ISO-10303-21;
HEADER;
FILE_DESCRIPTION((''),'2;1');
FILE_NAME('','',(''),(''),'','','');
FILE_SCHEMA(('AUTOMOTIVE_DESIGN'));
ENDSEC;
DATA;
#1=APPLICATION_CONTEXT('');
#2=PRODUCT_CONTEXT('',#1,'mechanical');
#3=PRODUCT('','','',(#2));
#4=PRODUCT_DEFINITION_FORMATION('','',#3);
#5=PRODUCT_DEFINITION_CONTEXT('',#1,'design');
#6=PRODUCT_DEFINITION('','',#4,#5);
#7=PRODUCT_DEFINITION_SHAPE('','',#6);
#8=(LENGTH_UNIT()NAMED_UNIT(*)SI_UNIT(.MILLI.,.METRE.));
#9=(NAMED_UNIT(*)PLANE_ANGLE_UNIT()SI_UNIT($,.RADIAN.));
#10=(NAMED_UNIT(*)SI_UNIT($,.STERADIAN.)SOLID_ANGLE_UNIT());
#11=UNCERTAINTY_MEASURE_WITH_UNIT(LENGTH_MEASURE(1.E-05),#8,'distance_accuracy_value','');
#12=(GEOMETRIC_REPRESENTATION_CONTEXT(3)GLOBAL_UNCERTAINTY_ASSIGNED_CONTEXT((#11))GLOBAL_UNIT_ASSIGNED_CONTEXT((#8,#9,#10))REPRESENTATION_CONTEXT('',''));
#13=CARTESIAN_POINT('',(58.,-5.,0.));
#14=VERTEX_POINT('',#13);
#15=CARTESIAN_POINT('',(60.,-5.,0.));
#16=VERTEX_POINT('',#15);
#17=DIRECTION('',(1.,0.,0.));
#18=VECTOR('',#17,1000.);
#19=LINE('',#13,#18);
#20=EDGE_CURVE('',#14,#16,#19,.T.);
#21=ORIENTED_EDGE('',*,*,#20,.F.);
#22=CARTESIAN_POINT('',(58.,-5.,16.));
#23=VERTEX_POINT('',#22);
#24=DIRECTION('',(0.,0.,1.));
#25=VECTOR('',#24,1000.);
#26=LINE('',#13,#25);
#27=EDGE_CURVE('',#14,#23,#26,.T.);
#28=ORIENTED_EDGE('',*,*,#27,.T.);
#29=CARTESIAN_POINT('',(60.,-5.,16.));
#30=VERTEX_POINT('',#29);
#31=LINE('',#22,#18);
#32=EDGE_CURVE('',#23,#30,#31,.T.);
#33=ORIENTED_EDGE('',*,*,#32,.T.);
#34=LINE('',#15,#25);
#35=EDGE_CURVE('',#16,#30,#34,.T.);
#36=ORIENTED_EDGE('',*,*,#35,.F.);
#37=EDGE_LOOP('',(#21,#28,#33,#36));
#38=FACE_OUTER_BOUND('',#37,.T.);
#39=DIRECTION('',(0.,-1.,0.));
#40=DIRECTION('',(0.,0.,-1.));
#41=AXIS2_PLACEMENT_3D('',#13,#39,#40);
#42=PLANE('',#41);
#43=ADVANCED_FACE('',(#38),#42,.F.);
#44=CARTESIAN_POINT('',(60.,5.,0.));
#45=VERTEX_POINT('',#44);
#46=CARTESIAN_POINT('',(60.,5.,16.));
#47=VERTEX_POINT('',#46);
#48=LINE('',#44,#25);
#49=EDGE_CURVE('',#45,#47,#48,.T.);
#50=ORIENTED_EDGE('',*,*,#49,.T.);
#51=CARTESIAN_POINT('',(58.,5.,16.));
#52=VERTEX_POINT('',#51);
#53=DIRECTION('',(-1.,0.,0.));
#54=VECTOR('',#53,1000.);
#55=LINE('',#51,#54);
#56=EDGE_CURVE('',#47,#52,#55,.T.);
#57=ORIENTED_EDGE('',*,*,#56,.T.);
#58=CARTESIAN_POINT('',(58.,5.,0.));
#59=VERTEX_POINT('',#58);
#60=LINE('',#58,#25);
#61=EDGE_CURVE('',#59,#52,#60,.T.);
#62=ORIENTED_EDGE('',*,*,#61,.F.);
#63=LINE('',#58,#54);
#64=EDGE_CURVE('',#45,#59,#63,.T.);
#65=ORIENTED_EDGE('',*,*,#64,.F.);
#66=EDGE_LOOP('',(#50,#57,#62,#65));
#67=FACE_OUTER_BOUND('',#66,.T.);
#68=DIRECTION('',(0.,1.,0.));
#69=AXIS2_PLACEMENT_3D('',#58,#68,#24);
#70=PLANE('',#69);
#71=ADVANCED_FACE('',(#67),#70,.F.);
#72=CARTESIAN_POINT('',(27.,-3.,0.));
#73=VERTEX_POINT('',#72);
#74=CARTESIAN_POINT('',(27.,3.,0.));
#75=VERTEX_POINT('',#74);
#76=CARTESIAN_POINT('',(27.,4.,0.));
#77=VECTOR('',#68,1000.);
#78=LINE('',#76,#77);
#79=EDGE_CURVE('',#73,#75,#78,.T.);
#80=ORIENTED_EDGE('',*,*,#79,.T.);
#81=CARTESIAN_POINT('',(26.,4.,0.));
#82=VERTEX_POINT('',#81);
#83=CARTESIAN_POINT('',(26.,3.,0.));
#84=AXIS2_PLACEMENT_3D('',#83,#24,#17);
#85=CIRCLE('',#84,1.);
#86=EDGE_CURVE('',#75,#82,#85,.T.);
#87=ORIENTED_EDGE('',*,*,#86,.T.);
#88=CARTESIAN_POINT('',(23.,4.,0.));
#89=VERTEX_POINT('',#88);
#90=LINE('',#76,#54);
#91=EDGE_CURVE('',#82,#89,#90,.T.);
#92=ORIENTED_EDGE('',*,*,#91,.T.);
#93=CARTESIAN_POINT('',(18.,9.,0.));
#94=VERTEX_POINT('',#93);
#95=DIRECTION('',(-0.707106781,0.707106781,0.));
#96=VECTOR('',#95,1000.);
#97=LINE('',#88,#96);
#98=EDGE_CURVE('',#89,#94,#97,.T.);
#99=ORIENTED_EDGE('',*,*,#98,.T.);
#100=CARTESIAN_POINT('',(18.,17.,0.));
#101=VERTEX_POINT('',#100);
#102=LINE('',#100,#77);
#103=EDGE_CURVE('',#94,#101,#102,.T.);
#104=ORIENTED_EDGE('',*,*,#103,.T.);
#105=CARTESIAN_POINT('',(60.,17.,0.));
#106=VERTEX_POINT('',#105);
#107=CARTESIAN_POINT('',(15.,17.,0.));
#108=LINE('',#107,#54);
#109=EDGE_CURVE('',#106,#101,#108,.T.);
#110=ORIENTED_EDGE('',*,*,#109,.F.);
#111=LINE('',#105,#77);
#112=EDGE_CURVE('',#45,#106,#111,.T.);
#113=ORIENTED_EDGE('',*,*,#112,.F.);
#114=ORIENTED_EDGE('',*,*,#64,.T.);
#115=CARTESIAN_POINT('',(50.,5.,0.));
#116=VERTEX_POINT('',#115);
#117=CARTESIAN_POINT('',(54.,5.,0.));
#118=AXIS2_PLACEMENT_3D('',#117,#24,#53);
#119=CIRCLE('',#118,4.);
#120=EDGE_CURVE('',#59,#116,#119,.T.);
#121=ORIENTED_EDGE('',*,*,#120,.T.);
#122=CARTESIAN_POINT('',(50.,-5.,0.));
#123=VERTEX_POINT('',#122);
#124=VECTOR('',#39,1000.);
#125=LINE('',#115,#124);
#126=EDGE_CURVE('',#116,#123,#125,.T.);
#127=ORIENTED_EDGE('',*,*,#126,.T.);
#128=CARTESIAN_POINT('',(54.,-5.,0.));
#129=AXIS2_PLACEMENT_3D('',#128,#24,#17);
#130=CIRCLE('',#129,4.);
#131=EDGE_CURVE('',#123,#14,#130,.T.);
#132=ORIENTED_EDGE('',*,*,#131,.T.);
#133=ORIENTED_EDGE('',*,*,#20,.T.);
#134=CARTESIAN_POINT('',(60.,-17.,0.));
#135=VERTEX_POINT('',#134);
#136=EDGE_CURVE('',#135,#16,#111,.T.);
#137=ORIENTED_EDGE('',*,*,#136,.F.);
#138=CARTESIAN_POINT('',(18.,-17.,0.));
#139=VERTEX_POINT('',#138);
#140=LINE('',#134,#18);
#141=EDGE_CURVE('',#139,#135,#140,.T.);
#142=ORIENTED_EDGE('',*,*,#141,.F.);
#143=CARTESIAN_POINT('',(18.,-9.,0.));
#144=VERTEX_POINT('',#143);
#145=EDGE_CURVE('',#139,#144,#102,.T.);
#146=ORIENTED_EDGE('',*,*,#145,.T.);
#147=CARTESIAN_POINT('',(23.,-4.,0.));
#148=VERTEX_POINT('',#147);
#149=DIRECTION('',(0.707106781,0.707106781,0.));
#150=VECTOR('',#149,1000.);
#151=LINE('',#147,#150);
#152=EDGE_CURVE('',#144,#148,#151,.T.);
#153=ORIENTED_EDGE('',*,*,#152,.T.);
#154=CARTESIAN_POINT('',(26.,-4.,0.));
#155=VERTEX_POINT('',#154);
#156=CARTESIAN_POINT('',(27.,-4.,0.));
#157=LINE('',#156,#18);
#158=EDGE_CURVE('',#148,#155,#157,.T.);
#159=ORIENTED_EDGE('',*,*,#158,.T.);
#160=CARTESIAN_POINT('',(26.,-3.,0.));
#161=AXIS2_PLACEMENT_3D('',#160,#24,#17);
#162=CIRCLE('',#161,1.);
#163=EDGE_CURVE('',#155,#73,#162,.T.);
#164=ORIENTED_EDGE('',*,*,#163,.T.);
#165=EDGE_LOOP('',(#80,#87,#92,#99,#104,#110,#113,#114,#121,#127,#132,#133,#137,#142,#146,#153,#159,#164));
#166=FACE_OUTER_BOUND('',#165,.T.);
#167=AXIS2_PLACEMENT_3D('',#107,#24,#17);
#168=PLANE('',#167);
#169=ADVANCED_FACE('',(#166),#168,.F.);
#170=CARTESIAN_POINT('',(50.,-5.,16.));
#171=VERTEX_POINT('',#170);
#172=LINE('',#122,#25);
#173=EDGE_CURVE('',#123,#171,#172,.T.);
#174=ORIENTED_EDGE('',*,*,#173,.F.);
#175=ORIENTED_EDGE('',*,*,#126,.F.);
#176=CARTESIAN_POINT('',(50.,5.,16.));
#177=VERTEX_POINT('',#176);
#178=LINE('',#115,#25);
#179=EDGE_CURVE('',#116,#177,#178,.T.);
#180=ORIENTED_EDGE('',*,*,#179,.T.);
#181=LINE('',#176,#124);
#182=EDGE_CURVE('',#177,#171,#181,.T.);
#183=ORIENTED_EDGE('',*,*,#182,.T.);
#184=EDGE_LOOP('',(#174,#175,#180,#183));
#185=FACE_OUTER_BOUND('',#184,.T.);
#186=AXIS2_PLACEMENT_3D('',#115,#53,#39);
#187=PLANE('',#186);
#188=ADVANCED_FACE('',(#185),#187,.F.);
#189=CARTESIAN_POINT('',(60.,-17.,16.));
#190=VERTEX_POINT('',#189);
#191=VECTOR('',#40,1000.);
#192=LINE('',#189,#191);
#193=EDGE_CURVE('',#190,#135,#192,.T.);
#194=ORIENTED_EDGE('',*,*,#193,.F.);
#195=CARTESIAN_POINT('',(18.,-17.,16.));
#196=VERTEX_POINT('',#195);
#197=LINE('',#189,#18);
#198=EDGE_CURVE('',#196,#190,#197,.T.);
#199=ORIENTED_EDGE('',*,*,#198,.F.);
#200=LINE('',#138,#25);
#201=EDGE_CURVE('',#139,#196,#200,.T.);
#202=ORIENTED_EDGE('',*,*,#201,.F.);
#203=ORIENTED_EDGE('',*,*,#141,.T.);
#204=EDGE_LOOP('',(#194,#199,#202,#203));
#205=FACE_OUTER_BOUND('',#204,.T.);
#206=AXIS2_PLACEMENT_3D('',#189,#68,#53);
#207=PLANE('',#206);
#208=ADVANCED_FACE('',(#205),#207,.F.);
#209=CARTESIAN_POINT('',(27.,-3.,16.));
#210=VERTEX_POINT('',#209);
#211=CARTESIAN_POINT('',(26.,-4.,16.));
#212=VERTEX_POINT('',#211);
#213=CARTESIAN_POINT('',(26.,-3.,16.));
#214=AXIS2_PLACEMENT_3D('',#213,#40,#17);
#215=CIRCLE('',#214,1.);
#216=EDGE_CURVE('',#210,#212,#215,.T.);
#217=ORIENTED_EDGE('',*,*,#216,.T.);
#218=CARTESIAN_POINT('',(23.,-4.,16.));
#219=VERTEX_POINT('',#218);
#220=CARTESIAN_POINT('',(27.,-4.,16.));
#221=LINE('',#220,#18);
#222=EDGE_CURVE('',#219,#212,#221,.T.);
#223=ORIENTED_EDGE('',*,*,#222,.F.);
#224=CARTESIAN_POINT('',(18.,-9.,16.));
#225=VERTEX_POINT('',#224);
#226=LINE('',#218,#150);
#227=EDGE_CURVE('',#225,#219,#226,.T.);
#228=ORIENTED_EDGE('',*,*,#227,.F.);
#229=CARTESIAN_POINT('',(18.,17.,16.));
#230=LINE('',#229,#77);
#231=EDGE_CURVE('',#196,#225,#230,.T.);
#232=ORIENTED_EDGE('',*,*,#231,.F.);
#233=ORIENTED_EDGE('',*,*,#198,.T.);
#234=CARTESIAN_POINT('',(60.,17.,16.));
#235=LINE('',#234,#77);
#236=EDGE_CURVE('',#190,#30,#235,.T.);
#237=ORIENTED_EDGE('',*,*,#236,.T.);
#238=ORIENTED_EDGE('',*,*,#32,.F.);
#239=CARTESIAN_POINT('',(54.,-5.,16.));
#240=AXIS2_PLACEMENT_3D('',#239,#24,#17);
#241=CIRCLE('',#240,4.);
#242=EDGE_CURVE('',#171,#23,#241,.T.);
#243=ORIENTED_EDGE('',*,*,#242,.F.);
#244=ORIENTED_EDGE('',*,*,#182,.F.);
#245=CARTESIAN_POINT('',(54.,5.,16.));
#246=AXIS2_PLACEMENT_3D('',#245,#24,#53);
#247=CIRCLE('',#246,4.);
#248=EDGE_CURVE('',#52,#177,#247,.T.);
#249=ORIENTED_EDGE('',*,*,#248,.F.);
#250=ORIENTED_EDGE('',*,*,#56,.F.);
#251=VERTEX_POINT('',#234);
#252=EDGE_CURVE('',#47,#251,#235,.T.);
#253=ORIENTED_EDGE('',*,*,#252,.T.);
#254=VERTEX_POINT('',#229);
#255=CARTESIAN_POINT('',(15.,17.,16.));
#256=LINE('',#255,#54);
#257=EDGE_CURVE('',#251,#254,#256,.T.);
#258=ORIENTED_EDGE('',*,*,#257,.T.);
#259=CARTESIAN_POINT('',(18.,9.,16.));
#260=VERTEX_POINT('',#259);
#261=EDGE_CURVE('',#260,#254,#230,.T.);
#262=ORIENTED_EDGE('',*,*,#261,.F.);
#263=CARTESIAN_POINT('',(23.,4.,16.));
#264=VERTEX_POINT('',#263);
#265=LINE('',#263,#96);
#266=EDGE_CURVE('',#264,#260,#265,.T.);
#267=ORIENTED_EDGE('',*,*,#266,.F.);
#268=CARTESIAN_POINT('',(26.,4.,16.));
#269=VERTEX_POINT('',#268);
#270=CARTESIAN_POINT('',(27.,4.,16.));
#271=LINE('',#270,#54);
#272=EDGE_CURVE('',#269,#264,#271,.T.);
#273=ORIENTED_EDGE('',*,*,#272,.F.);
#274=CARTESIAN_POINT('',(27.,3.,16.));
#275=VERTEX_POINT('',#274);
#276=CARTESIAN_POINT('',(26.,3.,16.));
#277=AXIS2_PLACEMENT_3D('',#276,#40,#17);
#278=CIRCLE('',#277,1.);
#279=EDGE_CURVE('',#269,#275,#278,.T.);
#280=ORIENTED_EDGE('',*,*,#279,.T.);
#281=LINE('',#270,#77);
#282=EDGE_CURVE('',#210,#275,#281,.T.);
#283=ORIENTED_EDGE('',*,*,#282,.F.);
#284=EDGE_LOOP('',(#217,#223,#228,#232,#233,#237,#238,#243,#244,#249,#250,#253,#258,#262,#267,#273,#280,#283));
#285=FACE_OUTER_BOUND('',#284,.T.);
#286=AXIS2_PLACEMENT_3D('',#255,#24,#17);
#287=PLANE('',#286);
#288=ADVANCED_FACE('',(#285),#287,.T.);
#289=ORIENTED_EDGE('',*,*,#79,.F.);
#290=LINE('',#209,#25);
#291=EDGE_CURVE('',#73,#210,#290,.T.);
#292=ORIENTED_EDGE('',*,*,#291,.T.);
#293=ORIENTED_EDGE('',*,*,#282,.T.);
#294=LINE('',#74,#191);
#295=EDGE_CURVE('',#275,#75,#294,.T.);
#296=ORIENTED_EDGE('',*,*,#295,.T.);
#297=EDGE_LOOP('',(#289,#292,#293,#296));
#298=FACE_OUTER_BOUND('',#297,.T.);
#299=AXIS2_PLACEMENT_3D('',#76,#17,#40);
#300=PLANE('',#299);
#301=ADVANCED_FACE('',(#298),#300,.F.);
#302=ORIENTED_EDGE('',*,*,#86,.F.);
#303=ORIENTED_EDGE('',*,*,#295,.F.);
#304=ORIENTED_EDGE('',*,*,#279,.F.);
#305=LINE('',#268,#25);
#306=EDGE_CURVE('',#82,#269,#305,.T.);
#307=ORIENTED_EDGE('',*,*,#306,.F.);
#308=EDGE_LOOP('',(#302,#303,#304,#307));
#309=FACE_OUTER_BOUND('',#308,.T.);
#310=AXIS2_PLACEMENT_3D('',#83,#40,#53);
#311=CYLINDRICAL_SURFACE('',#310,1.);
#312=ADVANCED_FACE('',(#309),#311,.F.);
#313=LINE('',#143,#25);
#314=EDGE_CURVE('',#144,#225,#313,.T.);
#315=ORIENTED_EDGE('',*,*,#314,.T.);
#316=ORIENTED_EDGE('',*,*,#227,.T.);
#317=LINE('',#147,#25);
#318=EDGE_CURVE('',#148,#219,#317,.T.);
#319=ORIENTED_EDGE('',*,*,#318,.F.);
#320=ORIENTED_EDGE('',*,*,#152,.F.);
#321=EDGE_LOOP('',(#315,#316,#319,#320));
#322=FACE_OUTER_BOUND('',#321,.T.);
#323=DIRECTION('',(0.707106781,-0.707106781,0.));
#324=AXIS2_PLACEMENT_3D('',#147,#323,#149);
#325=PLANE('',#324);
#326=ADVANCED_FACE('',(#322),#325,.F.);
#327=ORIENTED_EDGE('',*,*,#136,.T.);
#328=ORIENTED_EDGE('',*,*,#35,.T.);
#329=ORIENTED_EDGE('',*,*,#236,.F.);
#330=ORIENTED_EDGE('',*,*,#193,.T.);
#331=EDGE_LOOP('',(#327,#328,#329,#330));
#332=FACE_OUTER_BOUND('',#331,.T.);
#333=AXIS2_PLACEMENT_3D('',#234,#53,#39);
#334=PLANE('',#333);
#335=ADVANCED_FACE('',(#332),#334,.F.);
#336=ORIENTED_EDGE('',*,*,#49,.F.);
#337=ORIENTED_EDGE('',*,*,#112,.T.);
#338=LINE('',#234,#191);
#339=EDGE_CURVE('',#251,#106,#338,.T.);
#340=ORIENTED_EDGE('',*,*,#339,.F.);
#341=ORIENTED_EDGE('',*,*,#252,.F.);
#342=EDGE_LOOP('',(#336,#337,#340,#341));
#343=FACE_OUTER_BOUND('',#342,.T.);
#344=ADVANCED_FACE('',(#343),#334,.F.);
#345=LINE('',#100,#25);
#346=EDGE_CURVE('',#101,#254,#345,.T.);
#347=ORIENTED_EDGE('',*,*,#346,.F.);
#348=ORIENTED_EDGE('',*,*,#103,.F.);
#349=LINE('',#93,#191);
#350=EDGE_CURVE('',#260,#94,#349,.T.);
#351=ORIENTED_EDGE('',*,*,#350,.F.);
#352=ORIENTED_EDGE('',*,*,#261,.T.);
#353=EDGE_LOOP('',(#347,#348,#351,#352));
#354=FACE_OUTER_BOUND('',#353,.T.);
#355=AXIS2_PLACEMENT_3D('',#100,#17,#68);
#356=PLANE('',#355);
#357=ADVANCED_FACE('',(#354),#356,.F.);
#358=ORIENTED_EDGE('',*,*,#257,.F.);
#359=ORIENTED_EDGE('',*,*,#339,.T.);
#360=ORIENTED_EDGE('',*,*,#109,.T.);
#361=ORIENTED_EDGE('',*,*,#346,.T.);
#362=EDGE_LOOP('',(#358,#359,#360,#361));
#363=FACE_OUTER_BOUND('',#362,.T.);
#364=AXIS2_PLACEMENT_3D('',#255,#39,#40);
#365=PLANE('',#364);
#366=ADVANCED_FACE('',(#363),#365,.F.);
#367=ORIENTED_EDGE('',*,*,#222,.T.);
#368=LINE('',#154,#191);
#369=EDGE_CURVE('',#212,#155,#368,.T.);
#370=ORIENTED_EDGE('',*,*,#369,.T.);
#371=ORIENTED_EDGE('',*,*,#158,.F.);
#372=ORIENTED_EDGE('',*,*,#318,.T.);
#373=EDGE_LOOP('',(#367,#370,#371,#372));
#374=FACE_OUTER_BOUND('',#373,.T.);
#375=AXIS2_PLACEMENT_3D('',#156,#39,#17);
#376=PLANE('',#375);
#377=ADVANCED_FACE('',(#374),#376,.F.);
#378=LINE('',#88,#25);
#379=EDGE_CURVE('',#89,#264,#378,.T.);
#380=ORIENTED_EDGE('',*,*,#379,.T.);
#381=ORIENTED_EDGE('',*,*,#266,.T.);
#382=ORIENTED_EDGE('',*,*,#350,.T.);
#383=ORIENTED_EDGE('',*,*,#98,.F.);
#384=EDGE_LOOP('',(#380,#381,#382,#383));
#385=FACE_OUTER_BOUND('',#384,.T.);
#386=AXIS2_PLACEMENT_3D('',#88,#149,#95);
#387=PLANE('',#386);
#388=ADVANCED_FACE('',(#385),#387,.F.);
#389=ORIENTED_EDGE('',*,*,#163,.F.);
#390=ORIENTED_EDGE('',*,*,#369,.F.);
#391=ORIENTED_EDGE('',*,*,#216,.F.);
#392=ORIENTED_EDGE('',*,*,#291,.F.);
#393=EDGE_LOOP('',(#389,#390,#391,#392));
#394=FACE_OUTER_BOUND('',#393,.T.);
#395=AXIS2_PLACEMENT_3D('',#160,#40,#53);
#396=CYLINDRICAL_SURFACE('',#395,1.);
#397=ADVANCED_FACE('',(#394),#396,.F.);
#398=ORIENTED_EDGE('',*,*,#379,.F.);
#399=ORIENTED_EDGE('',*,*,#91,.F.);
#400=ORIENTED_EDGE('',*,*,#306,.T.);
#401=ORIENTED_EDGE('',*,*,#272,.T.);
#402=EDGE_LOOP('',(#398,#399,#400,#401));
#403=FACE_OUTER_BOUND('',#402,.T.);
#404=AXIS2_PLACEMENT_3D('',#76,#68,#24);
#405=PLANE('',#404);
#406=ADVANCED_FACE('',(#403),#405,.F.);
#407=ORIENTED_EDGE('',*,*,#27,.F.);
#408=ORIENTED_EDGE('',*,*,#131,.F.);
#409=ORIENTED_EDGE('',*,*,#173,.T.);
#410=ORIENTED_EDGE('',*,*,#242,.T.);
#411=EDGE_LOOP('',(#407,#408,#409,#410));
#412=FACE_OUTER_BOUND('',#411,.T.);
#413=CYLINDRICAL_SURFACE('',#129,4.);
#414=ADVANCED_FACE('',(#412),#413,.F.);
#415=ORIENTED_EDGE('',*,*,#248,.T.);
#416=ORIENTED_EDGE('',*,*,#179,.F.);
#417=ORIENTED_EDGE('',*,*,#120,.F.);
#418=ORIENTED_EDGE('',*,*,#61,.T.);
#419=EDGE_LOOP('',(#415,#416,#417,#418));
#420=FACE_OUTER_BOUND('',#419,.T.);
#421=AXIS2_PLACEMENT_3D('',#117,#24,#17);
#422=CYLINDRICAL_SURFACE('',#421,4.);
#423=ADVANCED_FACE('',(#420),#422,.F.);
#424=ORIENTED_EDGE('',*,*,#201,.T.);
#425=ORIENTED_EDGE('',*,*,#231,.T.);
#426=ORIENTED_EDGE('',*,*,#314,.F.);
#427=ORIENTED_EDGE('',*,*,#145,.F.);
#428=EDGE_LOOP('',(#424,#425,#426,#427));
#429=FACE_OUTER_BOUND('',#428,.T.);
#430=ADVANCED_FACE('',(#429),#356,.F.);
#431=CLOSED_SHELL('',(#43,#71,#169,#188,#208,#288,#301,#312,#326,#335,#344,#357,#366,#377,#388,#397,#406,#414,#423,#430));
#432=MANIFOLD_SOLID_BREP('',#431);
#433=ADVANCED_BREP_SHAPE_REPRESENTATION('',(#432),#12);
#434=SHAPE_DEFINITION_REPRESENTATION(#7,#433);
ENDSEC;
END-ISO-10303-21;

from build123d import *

# Parameters (mm, degrees)
SKETCH1_W          = 45
SKETCH1_H          = 34
BASE_EXTRUDE_DEPTH = 16
CUT_EXTRUDE1_DEPTH = 65.381674411
FILLET1_R          = 1
FILLET2_R          = 1
CUT_EXTRUDE3_DEPTH = 65.381674411
SKETCH5_W          = 3
SKETCH5_H          = 34
CUT_EXTRUDE4_DEPTH = 65.381674411


with BuildPart() as part:
    # Sketch1 → Base-Extrude (new body)
    with BuildSketch(Plane.XY):
        with Locations((37.5, 0)):
            Rectangle(SKETCH1_W, SKETCH1_H)
    extrude(amount=BASE_EXTRUDE_DEPTH)

    # Sketch2 → Cut-Extrude1 (cut, through all)
    with BuildSketch(Plane.XY.offset(16)):
        Polygon((27, 4), (27, -4), (23, -4), (15, -12), (15, 12), (23, 4), align=None)
    extrude(amount=-CUT_EXTRUDE1_DEPTH, mode=Mode.SUBTRACT)

    # Fillet1
    fillet1_edges = [part.edges().sort_by_distance(p)[0] for p in [
        (27, 4, 8),
    ]]
    fillet(fillet1_edges, radius=FILLET1_R)

    # Fillet2
    fillet2_edges = [part.edges().sort_by_distance(p)[0] for p in [
        (27, -4, 8),
    ]]
    fillet(fillet2_edges, radius=FILLET2_R)

    # Sketch4 → Cut-Extrude3 (cut, through all)
    with BuildSketch(Plane.XY.offset(16)):
        with BuildLine():
            Line((50, 5), (50, -5))
            ThreePointArc((50, -5), (54, -9), (58, -5))
            Line((58, -5), (60, -5))
            Line((60, -5), (60, 5))
            Line((60, 5), (58, 5))
            ThreePointArc((58, 5), (54, 9), (50, 5))
        make_face()
    extrude(amount=-CUT_EXTRUDE3_DEPTH, mode=Mode.SUBTRACT)

    # Sketch5 → Cut-Extrude4 (cut, through all)
    with BuildSketch(Plane.XY.offset(16)):
        with Locations((16.5, 0)):
            Rectangle(SKETCH5_W, SKETCH5_H)
    extrude(amount=-CUT_EXTRUDE4_DEPTH, mode=Mode.SUBTRACT)


solid = part.part
